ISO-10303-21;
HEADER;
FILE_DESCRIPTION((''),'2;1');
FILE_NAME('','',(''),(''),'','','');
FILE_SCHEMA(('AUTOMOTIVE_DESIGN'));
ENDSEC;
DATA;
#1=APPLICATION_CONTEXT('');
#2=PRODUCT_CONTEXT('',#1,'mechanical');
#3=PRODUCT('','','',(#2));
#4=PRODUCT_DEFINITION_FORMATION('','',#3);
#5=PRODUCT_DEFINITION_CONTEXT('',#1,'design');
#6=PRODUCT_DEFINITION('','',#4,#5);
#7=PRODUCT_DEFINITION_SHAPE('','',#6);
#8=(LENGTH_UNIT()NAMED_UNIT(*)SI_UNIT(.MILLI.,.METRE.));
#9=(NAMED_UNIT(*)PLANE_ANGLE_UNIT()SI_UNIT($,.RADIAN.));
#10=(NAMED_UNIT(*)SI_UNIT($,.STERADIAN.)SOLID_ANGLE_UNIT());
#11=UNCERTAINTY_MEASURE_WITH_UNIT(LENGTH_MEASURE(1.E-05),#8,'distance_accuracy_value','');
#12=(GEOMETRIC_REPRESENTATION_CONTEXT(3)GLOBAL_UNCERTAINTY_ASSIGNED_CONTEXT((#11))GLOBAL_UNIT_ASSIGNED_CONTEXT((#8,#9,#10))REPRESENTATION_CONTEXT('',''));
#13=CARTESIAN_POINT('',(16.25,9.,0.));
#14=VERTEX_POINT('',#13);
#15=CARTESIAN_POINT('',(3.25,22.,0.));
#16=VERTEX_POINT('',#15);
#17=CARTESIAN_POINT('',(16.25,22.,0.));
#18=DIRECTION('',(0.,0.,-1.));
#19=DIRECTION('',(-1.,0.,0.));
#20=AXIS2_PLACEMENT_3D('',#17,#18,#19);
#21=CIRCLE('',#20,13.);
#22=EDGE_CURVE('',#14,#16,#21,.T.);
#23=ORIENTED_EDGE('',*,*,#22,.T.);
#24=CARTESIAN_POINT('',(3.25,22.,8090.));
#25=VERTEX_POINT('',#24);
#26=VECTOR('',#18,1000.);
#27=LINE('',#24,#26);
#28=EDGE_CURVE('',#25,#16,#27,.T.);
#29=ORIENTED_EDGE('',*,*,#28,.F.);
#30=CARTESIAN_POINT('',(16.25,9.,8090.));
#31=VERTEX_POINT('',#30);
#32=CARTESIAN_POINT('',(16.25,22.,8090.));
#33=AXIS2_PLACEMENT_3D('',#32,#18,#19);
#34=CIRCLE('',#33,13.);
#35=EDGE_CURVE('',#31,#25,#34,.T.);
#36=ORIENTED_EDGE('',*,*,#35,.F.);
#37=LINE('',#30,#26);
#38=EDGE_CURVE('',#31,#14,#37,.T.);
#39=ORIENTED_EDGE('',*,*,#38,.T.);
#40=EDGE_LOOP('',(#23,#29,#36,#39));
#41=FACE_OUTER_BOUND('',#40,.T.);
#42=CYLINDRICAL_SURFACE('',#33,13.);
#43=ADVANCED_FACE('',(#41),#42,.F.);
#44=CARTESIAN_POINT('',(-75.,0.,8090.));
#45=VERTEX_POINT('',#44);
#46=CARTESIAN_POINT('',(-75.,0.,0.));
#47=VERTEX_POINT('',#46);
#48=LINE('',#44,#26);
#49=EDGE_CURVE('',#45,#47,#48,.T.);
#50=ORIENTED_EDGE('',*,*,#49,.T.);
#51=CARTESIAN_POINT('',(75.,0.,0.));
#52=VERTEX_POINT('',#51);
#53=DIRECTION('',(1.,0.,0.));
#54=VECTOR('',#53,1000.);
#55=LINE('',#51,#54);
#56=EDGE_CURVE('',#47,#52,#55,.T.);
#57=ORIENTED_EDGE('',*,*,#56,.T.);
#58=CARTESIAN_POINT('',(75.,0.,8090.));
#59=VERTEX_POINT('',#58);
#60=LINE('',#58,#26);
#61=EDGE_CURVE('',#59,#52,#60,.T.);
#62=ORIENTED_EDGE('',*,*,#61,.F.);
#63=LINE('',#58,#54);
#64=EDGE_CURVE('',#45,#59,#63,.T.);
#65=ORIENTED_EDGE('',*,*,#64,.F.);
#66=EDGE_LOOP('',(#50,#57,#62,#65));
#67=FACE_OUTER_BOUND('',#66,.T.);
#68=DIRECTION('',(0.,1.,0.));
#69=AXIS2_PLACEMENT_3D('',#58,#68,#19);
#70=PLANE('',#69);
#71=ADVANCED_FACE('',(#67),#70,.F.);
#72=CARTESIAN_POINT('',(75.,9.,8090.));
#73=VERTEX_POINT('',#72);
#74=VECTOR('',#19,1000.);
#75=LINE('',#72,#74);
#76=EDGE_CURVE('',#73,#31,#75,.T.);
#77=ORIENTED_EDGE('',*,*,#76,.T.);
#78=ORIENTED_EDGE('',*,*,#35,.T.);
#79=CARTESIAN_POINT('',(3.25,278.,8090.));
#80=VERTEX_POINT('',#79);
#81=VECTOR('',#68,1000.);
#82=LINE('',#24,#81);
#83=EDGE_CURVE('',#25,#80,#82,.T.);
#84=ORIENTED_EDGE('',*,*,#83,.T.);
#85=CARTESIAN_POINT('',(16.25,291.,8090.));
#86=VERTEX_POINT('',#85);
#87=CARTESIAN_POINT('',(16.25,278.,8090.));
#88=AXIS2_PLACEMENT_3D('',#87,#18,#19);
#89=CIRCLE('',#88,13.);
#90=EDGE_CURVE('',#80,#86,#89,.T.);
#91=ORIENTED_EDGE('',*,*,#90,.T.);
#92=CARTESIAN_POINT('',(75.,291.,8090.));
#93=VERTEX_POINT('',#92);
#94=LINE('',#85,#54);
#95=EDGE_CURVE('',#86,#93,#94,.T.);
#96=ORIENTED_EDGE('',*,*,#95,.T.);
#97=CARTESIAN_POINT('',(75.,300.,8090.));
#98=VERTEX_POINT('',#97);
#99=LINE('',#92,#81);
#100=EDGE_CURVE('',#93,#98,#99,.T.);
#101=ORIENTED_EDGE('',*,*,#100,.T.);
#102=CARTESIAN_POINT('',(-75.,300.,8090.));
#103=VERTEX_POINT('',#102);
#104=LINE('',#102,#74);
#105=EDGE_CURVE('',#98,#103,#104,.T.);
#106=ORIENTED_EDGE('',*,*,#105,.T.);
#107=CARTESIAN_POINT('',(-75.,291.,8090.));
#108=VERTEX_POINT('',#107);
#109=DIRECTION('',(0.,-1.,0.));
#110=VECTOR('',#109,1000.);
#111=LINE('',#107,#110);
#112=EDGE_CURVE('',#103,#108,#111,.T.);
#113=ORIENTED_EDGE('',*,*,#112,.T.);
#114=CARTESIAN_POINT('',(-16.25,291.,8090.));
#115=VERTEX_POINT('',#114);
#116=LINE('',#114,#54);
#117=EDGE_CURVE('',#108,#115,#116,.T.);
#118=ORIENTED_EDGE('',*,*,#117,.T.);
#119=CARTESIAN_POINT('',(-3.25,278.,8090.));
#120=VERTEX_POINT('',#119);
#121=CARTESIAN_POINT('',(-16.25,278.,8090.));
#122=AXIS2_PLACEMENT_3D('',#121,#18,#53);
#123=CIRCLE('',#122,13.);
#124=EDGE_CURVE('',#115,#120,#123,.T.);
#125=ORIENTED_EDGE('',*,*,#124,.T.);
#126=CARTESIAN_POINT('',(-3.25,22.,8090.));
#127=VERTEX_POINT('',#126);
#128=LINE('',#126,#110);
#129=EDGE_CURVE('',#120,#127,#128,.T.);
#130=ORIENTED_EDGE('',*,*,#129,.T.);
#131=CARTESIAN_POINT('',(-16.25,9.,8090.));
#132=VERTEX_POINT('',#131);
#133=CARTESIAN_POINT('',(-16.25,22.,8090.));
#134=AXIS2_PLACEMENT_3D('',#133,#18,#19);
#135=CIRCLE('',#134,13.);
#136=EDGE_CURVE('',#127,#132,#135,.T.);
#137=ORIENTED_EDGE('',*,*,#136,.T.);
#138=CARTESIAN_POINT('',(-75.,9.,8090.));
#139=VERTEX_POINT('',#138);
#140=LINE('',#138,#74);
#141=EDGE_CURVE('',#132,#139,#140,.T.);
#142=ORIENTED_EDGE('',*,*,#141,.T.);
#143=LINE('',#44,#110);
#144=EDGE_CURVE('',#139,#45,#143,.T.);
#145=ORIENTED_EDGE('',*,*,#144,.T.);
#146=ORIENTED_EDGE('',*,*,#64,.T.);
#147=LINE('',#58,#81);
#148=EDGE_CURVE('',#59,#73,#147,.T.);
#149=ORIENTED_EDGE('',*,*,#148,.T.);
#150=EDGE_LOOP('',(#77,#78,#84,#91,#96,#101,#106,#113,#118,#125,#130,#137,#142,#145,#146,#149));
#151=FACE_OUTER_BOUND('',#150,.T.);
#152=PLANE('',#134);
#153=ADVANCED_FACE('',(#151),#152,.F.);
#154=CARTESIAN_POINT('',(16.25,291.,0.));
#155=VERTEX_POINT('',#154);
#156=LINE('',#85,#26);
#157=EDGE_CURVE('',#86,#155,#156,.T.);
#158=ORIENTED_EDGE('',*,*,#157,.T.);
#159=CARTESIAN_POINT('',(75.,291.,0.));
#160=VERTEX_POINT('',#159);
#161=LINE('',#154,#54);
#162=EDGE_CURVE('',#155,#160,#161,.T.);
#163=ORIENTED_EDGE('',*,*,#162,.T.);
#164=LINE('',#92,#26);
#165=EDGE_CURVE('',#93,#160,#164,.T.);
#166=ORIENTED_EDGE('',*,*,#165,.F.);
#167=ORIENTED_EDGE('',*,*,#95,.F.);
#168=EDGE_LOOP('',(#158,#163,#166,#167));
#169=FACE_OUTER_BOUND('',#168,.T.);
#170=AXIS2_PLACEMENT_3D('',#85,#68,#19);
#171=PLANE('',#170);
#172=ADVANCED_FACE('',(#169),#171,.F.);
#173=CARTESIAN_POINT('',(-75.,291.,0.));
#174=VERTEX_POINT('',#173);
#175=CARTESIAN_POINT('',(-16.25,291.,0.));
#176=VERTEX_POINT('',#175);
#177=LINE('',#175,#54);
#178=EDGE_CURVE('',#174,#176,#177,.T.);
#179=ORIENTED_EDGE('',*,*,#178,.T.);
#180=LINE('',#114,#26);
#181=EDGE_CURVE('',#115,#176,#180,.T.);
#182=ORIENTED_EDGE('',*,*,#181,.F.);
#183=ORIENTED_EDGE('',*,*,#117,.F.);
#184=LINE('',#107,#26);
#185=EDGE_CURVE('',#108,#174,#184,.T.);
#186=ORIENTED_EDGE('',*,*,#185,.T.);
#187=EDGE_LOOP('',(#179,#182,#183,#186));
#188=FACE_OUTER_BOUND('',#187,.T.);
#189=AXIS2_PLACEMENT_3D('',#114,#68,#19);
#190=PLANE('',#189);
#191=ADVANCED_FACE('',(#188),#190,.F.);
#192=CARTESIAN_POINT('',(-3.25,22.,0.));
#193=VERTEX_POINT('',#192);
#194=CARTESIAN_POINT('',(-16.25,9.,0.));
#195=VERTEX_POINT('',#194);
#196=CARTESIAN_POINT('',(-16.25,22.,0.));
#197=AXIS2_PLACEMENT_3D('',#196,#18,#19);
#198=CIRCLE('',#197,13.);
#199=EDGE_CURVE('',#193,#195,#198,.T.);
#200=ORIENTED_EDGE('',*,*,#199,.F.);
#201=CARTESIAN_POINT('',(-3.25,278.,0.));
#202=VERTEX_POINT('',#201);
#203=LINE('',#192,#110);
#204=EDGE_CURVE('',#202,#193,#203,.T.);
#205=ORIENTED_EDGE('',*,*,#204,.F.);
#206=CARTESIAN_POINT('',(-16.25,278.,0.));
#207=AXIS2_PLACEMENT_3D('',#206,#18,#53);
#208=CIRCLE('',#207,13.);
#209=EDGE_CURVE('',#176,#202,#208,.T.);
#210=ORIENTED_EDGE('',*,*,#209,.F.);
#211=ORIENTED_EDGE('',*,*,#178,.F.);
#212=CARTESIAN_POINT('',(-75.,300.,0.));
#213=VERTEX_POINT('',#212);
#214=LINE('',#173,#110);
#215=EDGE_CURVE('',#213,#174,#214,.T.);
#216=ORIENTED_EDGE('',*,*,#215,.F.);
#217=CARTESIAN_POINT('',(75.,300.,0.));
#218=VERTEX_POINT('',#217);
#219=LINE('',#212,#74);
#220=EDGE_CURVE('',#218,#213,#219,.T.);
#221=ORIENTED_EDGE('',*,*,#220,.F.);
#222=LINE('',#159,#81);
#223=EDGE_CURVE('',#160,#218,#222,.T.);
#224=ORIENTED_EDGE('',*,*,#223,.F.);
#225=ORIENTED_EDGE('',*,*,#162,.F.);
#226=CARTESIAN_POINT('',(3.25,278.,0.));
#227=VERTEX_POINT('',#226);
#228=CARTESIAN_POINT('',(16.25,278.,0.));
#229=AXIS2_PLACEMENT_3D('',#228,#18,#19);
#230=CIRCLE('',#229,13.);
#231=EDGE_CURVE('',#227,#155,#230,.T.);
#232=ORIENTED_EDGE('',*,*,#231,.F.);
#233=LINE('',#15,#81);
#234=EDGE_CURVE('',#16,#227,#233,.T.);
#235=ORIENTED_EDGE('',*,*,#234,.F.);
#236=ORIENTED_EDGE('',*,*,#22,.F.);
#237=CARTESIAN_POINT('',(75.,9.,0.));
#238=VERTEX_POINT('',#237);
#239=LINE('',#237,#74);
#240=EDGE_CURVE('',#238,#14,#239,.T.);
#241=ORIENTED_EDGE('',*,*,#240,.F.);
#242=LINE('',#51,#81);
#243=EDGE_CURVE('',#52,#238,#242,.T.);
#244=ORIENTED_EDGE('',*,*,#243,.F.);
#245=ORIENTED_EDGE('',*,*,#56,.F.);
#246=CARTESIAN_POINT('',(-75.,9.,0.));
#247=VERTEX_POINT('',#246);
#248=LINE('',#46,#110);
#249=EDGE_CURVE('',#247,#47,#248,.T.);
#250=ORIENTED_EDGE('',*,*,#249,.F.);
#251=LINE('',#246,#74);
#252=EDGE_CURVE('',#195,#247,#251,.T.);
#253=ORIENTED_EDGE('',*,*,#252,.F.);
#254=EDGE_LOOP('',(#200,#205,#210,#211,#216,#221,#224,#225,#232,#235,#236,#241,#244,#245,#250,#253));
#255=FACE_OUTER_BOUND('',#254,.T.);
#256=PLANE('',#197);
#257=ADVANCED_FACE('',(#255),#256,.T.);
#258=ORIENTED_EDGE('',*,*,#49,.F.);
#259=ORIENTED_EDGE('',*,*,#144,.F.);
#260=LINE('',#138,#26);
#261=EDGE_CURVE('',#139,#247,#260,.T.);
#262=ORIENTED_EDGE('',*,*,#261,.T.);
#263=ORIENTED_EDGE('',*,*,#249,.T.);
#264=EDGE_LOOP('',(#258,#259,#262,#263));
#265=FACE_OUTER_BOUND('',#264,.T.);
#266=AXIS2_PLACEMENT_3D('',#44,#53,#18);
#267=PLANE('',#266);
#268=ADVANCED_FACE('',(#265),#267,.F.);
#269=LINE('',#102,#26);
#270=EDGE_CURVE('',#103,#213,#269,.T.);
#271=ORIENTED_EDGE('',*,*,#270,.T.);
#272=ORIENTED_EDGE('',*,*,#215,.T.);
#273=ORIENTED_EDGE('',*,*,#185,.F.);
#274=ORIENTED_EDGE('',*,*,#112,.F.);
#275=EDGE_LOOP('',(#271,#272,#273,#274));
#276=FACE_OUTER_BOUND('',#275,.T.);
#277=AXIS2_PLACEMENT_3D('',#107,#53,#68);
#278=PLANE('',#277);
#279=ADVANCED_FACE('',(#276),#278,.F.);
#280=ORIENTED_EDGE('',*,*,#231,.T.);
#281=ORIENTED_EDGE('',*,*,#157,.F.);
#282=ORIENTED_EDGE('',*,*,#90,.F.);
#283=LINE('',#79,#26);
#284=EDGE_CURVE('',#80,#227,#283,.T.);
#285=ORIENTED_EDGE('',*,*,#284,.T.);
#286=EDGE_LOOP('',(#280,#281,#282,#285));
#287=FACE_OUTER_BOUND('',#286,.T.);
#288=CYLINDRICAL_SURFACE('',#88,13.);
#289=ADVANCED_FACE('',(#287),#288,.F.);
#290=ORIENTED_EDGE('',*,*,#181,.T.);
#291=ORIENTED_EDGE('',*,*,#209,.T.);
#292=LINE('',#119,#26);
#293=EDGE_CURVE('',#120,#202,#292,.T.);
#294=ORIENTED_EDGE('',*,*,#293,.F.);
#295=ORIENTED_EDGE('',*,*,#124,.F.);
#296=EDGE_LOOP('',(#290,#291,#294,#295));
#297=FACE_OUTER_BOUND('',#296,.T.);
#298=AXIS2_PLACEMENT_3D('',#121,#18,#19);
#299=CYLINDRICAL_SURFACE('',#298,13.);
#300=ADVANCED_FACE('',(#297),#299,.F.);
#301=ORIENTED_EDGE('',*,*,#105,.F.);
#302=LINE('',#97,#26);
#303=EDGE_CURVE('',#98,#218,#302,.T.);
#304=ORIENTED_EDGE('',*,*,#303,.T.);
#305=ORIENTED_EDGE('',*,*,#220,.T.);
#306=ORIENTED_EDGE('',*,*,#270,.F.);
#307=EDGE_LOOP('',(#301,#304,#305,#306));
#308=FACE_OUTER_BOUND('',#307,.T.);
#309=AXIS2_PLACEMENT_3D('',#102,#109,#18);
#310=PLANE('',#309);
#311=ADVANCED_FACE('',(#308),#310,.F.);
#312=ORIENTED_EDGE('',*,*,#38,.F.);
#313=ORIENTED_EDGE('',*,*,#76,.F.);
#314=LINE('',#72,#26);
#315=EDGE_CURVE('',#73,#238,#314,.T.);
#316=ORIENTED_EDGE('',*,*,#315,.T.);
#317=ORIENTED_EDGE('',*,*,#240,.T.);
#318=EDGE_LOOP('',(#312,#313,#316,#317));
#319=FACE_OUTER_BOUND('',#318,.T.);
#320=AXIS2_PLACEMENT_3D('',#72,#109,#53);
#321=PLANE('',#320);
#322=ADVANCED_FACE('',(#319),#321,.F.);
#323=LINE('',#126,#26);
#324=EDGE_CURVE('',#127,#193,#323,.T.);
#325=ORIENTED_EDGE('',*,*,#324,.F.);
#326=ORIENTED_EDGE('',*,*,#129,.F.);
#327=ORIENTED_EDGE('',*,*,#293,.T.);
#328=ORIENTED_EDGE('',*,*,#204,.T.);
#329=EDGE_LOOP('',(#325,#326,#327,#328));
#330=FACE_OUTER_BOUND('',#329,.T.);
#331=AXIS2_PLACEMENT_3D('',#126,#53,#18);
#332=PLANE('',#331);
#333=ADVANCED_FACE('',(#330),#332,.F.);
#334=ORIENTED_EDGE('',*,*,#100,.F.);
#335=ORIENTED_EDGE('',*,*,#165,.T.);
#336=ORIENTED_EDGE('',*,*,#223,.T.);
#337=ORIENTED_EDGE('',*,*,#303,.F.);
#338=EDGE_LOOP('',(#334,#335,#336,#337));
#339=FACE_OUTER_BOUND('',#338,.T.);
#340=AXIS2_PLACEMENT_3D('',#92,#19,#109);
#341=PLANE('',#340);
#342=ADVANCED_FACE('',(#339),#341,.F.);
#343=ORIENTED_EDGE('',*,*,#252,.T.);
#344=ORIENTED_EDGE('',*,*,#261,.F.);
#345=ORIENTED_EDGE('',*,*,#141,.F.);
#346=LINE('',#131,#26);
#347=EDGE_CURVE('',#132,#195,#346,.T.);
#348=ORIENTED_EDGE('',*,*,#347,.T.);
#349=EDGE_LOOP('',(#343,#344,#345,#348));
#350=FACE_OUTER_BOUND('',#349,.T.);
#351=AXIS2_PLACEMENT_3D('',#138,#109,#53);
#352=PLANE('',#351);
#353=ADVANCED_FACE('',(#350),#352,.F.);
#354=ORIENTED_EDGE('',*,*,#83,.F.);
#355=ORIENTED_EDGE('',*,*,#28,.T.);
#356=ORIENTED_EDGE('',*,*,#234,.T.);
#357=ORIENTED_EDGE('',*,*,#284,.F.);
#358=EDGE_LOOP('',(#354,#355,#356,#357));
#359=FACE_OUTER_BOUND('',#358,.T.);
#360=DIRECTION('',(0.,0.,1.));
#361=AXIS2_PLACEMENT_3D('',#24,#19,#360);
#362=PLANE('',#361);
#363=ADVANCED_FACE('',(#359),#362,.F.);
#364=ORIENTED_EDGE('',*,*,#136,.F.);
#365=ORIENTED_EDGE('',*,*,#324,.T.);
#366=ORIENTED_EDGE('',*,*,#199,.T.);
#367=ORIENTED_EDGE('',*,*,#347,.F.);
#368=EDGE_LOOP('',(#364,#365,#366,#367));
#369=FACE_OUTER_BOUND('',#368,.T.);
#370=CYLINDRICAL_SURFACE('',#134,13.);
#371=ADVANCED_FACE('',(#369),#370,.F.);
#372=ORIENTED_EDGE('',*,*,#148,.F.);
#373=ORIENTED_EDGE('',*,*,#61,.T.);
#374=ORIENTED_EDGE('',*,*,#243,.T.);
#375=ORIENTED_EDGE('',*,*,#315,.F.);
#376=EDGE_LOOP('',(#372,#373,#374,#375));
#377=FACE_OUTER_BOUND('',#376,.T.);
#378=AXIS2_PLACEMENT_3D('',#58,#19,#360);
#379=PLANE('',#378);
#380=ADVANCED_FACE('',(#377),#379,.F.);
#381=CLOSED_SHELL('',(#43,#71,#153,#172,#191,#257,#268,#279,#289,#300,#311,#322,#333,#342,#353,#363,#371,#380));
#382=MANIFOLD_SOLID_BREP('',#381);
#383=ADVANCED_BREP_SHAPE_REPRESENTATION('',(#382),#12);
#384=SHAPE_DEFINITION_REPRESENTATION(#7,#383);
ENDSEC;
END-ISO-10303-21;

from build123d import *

# Parameters (mm, degrees)
BOSS_EXTRUDE1_DEPTH = 8090


with BuildPart() as part:
    # Sketch1 → Boss-Extrude1 (new body)
    with BuildSketch(Plane.XY):
        with BuildLine():
            Line((75, 0), (-75, 0))
            Line((-75, 0), (-75, 9))
            Line((-75, 9), (-16.25, 9))
            ThreePointArc((-16.25, 9), (-7.057611845, 12.807611845), (-3.25, 22))
            Line((-3.25, 22), (-3.25, 278))
            ThreePointArc((-3.25, 278), (-7.057611845, 287.192388155), (-16.25, 291))
            Line((-16.25, 291), (-75, 291))
            Line((-75, 291), (-75, 300))
            Line((-75, 300), (75, 300))
            Line((75, 300), (75, 291))
            Line((75, 291), (16.25, 291))
            ThreePointArc((16.25, 291), (7.057611845, 287.192388155), (3.25, 278))
            Line((3.25, 278), (3.25, 22))
            ThreePointArc((3.25, 22), (7.057611845, 12.807611845), (16.25, 9))
            Line((16.25, 9), (75, 9))
            Line((75, 9), (75, 0))
        make_face()
    extrude(amount=BOSS_EXTRUDE1_DEPTH)


solid = part.part
